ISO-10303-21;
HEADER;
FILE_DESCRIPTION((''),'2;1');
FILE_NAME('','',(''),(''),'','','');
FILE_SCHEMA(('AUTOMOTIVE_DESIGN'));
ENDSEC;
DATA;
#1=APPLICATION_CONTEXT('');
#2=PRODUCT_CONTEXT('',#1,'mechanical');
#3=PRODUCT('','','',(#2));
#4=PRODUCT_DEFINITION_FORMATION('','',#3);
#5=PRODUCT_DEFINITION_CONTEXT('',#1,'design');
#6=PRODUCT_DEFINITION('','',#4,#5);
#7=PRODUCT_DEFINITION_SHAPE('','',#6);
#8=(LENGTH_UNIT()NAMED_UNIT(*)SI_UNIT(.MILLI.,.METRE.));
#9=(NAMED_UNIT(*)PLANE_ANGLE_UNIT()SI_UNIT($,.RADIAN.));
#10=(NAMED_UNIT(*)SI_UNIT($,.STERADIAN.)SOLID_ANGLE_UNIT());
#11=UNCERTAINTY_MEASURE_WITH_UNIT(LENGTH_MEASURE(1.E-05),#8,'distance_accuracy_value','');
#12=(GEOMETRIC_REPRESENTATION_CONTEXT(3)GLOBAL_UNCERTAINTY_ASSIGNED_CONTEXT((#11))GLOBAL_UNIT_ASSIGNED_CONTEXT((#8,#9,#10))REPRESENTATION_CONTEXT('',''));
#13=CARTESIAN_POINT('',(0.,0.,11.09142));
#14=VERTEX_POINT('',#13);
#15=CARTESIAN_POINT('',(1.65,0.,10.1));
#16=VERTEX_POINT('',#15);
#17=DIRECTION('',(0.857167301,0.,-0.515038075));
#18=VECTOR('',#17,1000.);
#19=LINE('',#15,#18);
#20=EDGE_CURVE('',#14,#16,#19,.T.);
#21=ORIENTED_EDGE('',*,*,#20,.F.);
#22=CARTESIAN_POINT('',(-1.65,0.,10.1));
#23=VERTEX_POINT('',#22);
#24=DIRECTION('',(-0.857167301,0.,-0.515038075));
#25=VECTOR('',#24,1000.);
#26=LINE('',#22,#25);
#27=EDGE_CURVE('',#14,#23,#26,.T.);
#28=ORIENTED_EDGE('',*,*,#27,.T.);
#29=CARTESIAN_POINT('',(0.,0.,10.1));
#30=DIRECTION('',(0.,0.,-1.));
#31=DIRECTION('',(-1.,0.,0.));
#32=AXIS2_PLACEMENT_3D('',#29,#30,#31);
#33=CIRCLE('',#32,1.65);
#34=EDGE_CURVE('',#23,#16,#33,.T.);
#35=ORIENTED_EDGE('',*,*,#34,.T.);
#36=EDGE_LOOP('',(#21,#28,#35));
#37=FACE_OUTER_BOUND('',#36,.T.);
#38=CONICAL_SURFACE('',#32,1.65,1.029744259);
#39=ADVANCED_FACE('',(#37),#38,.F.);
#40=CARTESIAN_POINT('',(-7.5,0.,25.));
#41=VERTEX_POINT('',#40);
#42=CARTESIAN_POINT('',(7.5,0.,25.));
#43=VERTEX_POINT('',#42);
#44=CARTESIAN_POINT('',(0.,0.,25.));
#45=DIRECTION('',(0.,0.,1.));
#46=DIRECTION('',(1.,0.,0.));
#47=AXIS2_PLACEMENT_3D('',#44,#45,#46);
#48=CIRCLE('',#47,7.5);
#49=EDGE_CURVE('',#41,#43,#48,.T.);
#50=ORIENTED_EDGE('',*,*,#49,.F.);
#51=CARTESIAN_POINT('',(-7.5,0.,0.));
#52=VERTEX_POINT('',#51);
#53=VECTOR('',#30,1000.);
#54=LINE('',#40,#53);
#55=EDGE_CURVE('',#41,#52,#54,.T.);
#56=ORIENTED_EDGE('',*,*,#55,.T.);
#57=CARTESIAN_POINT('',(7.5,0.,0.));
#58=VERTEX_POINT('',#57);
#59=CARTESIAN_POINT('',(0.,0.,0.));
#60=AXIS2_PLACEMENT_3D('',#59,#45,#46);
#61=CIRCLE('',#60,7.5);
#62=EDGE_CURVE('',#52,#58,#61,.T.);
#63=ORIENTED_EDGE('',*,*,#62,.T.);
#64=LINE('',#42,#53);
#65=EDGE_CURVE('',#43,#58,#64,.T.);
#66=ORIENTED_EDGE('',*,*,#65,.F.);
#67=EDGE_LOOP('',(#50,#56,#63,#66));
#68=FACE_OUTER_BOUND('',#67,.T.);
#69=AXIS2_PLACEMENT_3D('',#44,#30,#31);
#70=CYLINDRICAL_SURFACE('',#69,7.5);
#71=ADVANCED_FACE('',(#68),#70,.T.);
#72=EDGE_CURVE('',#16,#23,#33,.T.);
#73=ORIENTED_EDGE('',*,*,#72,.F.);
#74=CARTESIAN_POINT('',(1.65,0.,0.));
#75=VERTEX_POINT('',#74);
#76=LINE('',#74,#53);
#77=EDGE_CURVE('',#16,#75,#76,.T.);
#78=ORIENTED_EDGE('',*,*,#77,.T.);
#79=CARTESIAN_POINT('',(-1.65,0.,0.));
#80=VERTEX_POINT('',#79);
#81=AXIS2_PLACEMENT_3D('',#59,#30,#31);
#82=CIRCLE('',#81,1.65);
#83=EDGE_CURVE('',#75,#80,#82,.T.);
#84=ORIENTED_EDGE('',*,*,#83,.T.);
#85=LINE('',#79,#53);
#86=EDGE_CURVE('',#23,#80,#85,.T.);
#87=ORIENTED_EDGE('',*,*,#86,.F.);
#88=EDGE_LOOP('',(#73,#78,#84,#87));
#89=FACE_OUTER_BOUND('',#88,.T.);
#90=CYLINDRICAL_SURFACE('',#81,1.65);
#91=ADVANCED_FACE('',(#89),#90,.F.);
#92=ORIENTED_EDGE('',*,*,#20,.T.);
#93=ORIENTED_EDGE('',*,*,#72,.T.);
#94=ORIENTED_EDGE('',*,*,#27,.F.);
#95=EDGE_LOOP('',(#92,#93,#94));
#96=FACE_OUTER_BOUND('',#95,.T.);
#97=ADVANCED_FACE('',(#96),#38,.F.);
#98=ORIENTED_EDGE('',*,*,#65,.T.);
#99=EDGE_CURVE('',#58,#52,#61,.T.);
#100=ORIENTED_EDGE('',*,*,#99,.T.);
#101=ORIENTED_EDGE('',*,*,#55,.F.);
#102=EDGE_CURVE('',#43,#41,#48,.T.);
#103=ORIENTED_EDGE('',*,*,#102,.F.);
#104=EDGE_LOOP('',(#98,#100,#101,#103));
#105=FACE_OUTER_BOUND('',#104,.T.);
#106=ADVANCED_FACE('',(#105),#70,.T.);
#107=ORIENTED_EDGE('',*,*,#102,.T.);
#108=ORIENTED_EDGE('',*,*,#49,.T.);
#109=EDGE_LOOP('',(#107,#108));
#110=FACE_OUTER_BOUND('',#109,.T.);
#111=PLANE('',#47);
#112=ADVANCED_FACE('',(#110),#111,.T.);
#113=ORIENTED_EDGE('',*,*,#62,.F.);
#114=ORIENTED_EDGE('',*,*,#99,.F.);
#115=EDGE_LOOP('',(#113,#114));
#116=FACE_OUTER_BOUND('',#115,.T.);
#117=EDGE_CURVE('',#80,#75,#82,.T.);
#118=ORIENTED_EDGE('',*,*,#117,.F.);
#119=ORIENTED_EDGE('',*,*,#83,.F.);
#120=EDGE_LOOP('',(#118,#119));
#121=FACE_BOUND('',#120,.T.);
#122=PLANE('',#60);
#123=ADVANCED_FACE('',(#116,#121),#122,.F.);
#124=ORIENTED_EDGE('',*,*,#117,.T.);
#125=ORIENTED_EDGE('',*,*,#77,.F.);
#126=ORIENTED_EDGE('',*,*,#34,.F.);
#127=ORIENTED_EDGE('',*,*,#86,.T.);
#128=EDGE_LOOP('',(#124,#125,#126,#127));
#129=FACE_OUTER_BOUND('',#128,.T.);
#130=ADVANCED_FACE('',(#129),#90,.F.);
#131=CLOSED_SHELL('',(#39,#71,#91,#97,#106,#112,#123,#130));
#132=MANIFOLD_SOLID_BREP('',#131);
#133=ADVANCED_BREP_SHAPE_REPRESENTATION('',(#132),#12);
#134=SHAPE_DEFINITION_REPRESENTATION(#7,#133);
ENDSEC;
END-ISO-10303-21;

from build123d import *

# Parameters (mm, degrees)
SKETCH_1_R             = 7.5
EXTRUDE_1_DEPTH        = 25
HOLE_WIZARD_M4_1_D     = 3.3
HOLE_WIZARD_M4_1_DEPTH = 10.1
HOLE_WIZARD_M4_1_TIP   = 0.991420021


with BuildPart() as part:
    # 草图1 → 凸台-拉伸1 (new body)
    with BuildSketch(Plane.XY):
        Circle(SKETCH_1_R)
    extrude(amount=EXTRUDE_1_DEPTH)

    # M4 螺纹孔1
    with Locations(Plane(origin=(0, 0, 0), x_dir=(-1, 0, 0), z_dir=(0, 0, -1))):
        with Locations((0, 0)):
            Hole(HOLE_WIZARD_M4_1_D / 2, depth=HOLE_WIZARD_M4_1_DEPTH)
            with Locations((0, 0, -(HOLE_WIZARD_M4_1_DEPTH + HOLE_WIZARD_M4_1_TIP / 2))):  # 118° drill point
                Cone(0, HOLE_WIZARD_M4_1_D / 2, HOLE_WIZARD_M4_1_TIP, mode=Mode.SUBTRACT)


solid = part.part
